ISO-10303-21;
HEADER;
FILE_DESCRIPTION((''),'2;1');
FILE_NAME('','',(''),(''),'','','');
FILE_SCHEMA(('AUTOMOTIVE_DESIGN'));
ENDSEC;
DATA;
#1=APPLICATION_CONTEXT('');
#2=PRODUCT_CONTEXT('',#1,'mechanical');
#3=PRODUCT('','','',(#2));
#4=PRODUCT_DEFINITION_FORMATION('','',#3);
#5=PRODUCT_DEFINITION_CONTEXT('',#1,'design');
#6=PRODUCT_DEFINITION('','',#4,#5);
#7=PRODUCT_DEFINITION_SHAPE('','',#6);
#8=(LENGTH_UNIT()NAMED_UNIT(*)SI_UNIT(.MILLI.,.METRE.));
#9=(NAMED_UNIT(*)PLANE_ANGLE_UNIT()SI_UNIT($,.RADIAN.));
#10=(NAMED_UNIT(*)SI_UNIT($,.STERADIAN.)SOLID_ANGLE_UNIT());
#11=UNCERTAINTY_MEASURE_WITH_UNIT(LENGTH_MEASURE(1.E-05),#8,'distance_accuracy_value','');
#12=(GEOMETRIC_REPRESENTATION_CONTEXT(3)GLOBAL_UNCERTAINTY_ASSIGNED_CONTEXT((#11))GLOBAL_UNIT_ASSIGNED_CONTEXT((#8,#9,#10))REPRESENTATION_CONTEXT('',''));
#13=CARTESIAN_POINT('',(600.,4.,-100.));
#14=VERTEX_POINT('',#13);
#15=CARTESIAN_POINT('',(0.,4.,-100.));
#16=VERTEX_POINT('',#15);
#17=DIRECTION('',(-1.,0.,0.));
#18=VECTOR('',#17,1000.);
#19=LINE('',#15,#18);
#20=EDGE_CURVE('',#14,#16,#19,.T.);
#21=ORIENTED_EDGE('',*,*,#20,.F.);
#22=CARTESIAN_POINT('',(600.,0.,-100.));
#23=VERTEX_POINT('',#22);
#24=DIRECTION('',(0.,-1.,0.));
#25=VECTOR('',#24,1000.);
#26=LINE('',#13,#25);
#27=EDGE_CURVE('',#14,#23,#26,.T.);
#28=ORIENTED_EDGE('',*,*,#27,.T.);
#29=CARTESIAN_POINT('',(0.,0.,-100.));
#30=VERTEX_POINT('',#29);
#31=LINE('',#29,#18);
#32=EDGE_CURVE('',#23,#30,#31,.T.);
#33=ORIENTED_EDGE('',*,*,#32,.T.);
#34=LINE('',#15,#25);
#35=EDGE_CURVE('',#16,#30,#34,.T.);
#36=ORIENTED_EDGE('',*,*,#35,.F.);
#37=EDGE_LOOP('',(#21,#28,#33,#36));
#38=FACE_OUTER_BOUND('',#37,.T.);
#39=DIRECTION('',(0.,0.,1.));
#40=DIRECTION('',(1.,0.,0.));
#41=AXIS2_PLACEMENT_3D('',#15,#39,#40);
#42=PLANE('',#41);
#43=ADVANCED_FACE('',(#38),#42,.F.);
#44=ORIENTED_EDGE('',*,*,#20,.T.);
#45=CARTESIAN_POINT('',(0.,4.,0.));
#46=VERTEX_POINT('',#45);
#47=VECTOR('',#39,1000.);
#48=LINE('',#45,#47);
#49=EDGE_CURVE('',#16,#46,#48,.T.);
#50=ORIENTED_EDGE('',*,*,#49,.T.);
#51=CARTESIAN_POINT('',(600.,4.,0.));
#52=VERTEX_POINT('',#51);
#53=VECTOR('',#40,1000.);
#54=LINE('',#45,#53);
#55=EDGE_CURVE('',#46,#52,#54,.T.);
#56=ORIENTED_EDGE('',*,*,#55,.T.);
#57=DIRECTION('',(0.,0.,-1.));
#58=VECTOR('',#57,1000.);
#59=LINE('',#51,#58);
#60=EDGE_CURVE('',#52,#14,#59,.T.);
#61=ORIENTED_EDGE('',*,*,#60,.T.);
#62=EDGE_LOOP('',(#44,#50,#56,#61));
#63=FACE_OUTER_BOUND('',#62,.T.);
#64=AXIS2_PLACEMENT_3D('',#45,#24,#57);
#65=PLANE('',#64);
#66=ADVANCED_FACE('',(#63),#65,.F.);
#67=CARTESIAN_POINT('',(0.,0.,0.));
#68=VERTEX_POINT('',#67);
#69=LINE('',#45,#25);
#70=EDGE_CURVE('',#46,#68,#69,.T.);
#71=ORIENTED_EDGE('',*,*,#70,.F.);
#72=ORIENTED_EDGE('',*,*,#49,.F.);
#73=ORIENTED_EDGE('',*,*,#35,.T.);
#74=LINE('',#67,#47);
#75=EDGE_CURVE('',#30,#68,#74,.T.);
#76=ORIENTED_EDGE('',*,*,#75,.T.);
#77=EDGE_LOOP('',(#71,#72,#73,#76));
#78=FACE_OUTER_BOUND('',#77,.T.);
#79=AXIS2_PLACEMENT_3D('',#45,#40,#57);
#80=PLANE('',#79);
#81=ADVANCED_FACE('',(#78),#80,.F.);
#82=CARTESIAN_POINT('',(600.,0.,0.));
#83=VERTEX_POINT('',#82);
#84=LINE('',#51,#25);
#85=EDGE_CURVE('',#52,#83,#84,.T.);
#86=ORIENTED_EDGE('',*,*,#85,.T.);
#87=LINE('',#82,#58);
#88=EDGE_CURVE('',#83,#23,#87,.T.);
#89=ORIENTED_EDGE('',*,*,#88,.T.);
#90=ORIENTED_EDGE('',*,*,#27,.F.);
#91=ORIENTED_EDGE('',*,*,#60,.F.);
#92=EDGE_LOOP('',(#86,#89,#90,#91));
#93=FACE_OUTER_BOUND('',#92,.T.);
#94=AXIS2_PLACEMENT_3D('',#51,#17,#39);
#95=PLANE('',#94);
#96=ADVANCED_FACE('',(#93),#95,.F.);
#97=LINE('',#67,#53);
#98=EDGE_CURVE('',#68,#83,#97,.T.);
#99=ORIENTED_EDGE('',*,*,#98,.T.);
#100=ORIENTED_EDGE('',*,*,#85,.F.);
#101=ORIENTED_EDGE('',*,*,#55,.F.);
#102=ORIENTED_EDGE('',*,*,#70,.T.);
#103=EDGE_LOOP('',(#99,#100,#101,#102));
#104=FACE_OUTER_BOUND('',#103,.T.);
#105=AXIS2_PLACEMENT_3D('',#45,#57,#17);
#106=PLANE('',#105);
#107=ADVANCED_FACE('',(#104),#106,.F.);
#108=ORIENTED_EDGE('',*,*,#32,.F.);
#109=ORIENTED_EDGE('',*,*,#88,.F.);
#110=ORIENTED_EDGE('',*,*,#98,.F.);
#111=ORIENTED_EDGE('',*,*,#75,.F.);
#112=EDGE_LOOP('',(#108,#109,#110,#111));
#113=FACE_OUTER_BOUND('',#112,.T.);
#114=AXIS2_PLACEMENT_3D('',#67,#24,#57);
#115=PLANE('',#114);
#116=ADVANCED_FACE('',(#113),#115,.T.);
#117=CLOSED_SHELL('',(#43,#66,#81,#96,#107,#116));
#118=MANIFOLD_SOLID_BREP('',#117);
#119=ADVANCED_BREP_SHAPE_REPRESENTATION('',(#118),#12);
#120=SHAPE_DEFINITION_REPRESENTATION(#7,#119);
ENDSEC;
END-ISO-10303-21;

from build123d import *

# Parameters (mm, degrees)
SKETCH_1_W      = 600
SKETCH_1_H      = 100
EXTRUDE_1_DEPTH = 4


with BuildPart() as part:
    # 草图1 → 凸台-拉伸1 (new body)
    with BuildSketch(Plane(origin=(0, 0, 0), x_dir=(1, 0, 0), z_dir=(0, 1, 0))):
        with Locations((300, 50)):
            Rectangle(SKETCH_1_W, SKETCH_1_H)
    extrude(amount=EXTRUDE_1_DEPTH)


solid = part.part
